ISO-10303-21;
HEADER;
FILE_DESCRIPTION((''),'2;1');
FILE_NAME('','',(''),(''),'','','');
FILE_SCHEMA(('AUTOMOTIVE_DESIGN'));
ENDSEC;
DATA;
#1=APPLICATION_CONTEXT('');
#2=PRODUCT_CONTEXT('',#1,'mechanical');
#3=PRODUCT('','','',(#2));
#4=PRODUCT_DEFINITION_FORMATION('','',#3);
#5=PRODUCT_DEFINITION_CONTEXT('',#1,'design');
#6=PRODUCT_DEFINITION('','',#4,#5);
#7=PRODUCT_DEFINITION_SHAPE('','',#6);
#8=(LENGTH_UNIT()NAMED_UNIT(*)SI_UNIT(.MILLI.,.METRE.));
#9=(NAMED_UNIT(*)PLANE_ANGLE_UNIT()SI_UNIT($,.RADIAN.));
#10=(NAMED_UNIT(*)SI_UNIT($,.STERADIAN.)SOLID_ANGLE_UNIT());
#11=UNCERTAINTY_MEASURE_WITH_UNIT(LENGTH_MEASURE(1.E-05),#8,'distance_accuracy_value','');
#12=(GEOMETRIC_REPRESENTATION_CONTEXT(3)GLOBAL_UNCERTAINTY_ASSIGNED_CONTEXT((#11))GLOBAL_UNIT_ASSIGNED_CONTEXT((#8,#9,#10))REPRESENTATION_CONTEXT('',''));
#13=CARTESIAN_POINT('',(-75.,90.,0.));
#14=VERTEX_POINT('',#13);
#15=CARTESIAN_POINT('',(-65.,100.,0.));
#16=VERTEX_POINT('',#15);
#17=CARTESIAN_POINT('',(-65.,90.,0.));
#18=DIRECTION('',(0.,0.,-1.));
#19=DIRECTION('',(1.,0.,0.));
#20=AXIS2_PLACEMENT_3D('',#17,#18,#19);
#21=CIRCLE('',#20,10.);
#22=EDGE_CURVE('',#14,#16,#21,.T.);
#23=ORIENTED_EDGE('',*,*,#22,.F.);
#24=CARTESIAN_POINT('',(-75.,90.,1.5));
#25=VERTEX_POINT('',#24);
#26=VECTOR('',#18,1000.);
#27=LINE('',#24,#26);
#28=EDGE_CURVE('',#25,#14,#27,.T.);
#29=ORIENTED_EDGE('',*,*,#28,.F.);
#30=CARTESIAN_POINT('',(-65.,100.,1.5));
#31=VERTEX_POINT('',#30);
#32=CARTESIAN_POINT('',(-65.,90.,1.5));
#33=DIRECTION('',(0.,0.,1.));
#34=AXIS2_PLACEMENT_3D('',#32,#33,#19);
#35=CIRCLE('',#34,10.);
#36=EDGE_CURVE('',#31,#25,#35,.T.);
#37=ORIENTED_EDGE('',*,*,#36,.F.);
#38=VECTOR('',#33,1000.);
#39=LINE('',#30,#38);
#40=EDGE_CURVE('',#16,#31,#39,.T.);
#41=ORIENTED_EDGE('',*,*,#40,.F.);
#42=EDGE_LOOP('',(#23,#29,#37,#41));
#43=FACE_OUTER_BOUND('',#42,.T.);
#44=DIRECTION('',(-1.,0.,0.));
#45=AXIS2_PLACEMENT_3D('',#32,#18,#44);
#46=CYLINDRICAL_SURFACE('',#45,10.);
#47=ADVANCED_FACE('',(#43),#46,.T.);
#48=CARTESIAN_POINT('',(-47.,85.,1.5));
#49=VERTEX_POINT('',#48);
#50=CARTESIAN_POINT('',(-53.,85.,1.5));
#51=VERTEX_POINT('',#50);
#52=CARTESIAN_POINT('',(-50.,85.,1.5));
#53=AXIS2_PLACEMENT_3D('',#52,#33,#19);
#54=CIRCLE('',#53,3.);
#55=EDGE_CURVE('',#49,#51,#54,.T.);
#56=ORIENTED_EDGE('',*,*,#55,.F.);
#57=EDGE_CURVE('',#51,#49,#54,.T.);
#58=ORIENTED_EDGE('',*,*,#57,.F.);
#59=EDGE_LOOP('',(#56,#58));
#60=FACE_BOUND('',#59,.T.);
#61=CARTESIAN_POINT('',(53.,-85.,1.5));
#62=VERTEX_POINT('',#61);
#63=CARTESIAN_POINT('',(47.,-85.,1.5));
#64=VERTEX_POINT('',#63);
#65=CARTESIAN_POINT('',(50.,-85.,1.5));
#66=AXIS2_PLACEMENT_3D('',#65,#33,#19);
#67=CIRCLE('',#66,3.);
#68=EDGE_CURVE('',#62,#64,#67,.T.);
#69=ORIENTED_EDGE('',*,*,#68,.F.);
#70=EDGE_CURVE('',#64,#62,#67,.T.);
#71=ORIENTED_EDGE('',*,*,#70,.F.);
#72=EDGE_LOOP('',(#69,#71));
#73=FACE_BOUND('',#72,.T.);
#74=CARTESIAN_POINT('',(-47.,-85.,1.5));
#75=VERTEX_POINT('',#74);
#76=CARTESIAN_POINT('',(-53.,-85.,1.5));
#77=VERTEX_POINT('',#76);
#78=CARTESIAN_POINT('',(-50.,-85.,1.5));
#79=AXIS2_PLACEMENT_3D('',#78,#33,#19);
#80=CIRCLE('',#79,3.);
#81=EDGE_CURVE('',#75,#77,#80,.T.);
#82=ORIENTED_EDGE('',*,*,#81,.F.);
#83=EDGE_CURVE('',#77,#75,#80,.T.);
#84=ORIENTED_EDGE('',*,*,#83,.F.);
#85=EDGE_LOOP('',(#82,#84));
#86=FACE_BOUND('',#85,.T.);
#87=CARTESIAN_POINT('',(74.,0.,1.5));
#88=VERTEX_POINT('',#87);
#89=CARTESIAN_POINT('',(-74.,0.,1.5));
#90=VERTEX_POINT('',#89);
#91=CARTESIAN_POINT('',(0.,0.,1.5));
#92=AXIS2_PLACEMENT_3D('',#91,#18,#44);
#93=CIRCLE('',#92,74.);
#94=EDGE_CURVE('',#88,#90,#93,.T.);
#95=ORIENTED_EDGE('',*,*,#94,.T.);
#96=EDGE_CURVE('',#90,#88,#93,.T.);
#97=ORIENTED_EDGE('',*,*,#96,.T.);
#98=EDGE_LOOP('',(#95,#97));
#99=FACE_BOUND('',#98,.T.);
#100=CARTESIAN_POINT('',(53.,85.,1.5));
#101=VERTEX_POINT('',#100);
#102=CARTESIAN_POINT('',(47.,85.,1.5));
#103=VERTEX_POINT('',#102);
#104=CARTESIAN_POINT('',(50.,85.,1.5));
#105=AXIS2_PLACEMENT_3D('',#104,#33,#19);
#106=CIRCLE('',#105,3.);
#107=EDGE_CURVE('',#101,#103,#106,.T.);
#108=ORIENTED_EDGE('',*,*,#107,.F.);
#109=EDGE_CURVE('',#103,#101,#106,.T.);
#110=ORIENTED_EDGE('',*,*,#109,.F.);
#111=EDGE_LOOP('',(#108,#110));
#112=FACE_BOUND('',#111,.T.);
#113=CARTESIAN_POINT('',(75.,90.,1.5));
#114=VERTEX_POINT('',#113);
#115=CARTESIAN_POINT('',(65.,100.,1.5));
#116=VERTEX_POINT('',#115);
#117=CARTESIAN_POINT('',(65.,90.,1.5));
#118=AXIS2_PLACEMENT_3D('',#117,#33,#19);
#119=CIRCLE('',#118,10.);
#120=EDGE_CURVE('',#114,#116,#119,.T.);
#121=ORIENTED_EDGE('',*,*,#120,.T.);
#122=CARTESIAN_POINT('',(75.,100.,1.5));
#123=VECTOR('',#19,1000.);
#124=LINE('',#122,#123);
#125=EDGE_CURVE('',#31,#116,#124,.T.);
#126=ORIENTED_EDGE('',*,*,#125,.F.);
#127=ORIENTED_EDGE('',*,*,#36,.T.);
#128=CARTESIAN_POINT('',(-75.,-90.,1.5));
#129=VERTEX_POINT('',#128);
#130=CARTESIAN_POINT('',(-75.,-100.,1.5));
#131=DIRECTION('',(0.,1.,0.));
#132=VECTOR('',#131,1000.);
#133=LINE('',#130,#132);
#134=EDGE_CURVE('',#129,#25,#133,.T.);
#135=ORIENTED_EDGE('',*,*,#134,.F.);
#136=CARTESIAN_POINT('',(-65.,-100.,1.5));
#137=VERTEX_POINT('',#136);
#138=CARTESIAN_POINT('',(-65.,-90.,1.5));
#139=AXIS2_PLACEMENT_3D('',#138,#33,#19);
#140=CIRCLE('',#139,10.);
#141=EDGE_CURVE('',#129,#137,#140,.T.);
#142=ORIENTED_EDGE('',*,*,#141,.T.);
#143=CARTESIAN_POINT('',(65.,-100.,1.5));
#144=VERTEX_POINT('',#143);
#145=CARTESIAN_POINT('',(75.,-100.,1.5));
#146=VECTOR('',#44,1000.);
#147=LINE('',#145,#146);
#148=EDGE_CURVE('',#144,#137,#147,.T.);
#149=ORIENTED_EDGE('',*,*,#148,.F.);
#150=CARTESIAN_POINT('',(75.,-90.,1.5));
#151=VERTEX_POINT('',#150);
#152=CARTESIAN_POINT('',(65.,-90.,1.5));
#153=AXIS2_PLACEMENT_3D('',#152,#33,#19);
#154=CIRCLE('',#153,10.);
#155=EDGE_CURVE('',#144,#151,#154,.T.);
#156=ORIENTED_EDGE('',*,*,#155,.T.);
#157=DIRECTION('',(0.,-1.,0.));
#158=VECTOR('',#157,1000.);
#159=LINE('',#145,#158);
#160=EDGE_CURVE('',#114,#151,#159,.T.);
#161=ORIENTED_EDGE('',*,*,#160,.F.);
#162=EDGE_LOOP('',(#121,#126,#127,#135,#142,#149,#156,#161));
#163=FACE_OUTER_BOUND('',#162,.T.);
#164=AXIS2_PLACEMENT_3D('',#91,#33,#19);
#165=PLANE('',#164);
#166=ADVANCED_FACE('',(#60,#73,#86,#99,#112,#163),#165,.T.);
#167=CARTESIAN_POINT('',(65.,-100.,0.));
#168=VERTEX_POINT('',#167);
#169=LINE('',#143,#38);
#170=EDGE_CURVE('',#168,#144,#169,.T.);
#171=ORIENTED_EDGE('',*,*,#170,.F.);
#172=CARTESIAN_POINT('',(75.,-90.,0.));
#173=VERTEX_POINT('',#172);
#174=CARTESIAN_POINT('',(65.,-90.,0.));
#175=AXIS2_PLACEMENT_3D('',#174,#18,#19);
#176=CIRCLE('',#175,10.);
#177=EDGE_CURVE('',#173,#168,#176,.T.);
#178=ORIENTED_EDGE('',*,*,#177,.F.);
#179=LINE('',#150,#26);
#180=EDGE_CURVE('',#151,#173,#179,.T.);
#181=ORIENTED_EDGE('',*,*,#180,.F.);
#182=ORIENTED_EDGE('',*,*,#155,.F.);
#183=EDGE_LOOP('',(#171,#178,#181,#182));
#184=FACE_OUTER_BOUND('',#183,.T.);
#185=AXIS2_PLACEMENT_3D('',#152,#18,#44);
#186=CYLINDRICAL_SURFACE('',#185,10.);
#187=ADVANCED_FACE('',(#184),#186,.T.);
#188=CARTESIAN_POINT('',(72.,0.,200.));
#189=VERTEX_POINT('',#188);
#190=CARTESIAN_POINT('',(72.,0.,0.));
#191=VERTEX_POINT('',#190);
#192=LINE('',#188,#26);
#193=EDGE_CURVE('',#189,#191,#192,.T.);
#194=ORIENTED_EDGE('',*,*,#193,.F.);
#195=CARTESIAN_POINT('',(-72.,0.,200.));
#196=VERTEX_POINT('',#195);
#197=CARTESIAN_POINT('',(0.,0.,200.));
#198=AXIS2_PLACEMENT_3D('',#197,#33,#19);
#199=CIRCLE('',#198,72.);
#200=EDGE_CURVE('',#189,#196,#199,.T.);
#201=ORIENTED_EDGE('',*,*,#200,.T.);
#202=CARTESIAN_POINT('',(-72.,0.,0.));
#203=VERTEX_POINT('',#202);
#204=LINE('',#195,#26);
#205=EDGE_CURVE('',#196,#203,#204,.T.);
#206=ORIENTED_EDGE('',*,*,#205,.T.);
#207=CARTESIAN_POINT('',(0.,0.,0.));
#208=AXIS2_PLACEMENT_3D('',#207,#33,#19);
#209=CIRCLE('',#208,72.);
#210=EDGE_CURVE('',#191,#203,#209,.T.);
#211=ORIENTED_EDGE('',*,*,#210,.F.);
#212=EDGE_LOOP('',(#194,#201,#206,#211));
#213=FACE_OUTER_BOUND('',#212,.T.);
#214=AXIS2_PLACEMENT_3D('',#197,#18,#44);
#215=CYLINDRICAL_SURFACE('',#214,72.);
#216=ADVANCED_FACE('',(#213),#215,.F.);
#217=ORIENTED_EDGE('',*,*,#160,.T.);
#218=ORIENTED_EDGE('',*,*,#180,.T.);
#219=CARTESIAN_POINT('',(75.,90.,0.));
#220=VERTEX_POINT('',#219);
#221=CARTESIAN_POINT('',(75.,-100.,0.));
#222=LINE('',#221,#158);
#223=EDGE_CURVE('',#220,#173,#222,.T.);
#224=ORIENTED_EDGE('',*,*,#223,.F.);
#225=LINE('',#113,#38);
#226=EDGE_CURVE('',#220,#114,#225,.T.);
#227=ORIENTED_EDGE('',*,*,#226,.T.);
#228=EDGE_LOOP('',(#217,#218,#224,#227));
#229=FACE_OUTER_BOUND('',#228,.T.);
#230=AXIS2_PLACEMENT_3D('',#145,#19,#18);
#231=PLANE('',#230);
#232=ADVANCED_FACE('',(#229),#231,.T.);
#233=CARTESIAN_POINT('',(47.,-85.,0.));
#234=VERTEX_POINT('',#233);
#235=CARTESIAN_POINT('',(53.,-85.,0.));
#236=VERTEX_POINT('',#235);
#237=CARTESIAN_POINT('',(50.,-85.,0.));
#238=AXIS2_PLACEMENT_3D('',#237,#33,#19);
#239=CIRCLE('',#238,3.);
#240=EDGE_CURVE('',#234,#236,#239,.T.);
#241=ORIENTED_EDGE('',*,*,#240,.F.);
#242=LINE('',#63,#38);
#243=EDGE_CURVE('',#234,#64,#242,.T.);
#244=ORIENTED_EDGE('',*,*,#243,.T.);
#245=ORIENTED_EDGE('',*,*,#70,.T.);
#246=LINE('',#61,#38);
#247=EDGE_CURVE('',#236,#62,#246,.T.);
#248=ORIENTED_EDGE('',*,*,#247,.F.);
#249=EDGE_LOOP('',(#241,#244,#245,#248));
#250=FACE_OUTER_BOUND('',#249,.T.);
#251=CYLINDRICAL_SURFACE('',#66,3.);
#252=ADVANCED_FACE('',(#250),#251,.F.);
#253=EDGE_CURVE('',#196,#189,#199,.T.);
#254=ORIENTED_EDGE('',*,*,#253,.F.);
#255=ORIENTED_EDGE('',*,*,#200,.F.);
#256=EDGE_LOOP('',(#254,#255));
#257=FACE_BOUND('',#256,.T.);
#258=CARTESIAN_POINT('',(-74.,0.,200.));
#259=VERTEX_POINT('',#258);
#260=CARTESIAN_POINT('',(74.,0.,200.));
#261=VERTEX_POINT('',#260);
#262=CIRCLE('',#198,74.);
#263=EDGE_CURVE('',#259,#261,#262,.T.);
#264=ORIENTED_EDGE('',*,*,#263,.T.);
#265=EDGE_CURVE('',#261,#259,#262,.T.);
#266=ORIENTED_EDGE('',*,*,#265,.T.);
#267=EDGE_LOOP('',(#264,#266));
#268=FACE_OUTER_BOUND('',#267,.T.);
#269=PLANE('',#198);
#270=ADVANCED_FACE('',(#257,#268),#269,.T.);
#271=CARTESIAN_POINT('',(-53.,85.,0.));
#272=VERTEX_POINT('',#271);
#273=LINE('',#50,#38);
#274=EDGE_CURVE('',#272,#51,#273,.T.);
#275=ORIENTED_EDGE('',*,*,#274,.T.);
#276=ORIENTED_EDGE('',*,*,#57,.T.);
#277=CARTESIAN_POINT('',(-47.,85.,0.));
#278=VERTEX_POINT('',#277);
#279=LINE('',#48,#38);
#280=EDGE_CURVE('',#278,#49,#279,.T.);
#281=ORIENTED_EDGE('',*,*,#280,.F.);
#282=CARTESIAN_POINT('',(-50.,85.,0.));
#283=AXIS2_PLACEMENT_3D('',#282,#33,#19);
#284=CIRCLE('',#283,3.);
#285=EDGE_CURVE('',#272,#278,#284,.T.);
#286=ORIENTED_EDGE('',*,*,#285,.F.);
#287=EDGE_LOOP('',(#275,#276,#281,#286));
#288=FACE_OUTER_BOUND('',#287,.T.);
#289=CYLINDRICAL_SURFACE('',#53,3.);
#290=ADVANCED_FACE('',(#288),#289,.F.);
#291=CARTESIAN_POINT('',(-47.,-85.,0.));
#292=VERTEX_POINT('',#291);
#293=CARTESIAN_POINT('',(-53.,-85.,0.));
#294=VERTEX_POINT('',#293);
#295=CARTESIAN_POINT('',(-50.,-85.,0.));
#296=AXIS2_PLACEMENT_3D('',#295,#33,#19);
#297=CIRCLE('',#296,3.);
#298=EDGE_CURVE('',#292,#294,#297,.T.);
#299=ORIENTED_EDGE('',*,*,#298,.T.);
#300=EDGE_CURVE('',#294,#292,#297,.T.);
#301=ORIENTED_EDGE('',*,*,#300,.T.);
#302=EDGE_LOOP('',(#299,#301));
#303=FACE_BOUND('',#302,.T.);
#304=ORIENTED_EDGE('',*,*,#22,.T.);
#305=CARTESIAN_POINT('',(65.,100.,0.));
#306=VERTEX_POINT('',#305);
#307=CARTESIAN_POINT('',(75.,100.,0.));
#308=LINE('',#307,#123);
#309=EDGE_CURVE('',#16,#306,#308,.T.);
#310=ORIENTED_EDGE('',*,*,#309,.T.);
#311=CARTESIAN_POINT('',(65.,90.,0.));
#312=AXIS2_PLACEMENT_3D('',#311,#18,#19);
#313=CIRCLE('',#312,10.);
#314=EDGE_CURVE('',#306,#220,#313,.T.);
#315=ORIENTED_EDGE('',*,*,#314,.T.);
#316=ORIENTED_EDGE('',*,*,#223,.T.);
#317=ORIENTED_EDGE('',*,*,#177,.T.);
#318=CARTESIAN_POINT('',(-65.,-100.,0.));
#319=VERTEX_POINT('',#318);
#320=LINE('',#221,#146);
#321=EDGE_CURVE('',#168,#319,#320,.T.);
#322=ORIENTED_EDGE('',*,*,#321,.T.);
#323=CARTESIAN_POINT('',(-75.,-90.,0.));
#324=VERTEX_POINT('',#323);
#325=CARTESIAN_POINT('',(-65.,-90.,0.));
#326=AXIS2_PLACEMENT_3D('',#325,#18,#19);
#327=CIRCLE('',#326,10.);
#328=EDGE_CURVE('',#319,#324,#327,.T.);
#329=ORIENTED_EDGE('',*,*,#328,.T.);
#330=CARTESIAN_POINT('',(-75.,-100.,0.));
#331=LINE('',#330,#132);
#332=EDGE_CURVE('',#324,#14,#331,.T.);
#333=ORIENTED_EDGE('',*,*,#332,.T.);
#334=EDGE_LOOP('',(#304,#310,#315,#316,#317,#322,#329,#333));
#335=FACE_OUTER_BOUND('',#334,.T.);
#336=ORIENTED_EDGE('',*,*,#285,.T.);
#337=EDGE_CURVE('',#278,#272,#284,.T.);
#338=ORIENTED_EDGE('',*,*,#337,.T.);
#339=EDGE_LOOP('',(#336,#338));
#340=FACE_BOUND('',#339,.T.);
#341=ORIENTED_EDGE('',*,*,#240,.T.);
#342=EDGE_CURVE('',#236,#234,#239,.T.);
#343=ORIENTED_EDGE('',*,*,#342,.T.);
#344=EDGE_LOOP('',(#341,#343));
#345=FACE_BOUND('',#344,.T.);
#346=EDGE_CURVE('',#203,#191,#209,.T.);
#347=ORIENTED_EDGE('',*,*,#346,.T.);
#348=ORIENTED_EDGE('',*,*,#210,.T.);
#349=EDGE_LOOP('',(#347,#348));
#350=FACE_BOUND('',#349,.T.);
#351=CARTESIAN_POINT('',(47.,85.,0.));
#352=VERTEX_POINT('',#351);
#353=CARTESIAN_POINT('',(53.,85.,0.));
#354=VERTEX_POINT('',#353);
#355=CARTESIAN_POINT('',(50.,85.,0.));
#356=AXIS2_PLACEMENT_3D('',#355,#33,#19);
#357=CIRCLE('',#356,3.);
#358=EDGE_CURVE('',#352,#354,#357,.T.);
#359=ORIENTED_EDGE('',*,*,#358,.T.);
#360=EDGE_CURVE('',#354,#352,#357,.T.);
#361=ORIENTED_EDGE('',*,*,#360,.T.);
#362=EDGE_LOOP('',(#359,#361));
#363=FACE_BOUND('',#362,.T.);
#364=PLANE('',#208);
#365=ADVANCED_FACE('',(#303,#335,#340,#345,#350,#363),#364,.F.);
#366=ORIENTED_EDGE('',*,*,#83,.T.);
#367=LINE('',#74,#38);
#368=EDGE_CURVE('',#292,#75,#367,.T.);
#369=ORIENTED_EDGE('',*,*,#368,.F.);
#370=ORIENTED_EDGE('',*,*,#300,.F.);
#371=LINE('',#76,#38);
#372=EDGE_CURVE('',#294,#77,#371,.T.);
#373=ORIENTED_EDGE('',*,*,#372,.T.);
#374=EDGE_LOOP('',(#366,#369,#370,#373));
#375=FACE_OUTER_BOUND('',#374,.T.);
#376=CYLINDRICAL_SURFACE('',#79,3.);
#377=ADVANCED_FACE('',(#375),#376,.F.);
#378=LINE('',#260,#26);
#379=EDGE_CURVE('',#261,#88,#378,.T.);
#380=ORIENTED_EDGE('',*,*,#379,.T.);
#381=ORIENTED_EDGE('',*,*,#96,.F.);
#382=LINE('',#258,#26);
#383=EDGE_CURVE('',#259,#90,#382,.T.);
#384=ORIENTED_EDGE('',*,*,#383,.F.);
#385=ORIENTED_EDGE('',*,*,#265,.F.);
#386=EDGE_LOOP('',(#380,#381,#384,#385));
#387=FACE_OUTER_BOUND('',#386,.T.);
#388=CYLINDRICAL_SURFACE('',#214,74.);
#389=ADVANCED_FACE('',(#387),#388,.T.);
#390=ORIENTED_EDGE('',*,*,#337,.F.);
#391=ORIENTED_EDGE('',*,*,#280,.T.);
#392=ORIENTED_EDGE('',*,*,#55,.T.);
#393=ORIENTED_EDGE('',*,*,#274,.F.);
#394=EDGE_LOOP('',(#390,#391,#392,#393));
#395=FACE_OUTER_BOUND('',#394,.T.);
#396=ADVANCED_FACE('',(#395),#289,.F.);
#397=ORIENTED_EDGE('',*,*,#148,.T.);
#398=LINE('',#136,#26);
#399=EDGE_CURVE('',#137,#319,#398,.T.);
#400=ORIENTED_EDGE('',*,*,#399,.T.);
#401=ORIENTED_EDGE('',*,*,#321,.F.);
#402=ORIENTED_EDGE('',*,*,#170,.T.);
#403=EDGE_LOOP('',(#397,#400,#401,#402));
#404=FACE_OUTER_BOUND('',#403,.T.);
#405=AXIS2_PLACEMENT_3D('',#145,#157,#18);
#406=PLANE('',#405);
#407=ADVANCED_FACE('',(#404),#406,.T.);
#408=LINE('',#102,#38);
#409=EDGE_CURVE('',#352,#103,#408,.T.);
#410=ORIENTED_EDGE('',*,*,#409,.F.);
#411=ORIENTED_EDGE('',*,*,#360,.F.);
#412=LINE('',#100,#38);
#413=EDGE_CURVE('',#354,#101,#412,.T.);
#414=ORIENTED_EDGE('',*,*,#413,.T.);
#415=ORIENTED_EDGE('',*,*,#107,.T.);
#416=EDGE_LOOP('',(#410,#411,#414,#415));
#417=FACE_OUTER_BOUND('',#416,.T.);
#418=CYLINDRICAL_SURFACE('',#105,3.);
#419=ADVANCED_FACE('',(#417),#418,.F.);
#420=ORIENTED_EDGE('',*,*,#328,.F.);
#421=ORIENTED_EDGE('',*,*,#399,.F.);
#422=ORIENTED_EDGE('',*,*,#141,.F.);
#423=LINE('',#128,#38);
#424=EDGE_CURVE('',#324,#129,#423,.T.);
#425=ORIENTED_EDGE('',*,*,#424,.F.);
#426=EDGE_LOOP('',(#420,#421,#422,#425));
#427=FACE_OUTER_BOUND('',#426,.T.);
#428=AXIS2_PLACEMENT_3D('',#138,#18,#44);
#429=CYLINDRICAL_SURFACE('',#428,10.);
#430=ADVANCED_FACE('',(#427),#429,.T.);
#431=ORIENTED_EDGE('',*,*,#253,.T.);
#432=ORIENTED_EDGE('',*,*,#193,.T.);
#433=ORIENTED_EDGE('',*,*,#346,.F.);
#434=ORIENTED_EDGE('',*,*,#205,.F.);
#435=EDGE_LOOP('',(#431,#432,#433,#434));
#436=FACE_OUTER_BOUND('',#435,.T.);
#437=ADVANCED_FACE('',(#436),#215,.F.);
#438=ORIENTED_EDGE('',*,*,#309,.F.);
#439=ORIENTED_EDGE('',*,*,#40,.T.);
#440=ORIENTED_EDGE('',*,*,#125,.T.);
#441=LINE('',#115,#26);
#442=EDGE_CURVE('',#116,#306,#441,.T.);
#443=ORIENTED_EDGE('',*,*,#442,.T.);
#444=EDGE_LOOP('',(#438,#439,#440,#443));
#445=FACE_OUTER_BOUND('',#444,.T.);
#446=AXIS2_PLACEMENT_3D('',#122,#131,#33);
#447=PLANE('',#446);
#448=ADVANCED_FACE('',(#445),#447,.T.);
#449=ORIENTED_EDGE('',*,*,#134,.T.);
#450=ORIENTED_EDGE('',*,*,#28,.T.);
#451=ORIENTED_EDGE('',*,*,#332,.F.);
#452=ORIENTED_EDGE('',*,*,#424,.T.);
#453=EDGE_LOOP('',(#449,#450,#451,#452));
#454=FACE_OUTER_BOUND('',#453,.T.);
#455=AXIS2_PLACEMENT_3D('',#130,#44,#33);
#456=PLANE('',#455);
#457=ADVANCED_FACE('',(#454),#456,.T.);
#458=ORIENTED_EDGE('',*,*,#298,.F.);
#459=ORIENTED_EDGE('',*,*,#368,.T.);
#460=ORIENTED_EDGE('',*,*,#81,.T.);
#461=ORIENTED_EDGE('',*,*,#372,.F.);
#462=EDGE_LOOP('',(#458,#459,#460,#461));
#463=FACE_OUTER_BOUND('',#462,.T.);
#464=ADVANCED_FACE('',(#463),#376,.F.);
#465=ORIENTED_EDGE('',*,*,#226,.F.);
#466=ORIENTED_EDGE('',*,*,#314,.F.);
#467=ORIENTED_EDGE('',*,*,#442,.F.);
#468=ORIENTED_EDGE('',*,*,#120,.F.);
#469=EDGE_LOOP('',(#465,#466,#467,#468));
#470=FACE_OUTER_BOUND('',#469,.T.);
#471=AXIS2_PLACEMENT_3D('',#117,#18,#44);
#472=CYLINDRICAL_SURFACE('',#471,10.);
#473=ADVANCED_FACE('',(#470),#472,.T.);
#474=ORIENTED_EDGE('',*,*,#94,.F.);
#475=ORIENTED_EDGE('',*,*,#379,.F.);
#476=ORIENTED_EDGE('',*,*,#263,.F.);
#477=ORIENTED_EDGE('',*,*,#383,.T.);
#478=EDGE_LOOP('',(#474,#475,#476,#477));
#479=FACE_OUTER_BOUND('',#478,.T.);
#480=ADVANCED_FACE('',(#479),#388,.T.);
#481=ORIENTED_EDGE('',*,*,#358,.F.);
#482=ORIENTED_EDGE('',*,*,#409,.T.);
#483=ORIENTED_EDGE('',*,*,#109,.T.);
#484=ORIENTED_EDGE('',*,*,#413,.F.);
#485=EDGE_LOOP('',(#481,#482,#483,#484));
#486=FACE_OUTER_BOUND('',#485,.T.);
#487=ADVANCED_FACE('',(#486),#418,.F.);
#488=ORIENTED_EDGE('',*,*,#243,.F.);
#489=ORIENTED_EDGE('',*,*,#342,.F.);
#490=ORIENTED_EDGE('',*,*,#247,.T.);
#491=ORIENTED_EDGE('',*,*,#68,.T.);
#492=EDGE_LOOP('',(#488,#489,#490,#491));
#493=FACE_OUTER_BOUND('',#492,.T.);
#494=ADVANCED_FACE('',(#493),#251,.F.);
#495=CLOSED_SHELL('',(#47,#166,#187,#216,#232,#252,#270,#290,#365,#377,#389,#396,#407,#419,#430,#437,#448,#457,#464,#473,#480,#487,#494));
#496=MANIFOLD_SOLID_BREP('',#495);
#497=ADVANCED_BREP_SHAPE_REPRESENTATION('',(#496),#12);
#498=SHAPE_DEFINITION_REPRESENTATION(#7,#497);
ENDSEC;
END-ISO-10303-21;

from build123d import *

# Parameters (mm, degrees)
SKETCH_1_R            = 74
SKETCH_1_R_2          = 72
EXTRUDE_1_DEPTH       = 200
SKETCH_2_W            = 150
SKETCH_2_H            = 200
SKETCH_2_R            = 74
EXTRUDE_2_DEPTH       = 1.5
FILLET_1_R            = 10
HOLE_WIZARD_6_0_6_1_D = 6


with BuildPart() as part:
    # 草图1 → 凸台-拉伸1 (new body)
    with BuildSketch(Plane.XY):
        Circle(SKETCH_1_R)
        Circle(SKETCH_1_R_2, mode=Mode.SUBTRACT)
    extrude(amount=EXTRUDE_1_DEPTH)

    # 草图2 → 凸台-拉伸2 (add)
    with BuildSketch(Plane(origin=(0, 0, 0), x_dir=(-1, 0, 0), z_dir=(0, 0, -1))):
        Rectangle(SKETCH_2_W, SKETCH_2_H)
        Circle(SKETCH_2_R, mode=Mode.SUBTRACT)
    extrude(amount=-EXTRUDE_2_DEPTH)

    # 圆角1
    fillet_1_edges = [part.edges().sort_by_distance(p)[0] for p in [
        (-75, 100, 0.75),
        (-75, -100, 0.75),
        (75, -100, 0.75),
        (75, 100, 0.75),
    ]]
    fillet(fillet_1_edges, radius=FILLET_1_R)

    # Ø6.0 (6) 直径孔1 (through all)
    with Locations(Plane.XY.offset(1.5)):
        with Locations((-50, -85), (-50, 85), (50, 85), (50, -85)):
            Hole(HOLE_WIZARD_6_0_6_1_D / 2)


solid = part.part
